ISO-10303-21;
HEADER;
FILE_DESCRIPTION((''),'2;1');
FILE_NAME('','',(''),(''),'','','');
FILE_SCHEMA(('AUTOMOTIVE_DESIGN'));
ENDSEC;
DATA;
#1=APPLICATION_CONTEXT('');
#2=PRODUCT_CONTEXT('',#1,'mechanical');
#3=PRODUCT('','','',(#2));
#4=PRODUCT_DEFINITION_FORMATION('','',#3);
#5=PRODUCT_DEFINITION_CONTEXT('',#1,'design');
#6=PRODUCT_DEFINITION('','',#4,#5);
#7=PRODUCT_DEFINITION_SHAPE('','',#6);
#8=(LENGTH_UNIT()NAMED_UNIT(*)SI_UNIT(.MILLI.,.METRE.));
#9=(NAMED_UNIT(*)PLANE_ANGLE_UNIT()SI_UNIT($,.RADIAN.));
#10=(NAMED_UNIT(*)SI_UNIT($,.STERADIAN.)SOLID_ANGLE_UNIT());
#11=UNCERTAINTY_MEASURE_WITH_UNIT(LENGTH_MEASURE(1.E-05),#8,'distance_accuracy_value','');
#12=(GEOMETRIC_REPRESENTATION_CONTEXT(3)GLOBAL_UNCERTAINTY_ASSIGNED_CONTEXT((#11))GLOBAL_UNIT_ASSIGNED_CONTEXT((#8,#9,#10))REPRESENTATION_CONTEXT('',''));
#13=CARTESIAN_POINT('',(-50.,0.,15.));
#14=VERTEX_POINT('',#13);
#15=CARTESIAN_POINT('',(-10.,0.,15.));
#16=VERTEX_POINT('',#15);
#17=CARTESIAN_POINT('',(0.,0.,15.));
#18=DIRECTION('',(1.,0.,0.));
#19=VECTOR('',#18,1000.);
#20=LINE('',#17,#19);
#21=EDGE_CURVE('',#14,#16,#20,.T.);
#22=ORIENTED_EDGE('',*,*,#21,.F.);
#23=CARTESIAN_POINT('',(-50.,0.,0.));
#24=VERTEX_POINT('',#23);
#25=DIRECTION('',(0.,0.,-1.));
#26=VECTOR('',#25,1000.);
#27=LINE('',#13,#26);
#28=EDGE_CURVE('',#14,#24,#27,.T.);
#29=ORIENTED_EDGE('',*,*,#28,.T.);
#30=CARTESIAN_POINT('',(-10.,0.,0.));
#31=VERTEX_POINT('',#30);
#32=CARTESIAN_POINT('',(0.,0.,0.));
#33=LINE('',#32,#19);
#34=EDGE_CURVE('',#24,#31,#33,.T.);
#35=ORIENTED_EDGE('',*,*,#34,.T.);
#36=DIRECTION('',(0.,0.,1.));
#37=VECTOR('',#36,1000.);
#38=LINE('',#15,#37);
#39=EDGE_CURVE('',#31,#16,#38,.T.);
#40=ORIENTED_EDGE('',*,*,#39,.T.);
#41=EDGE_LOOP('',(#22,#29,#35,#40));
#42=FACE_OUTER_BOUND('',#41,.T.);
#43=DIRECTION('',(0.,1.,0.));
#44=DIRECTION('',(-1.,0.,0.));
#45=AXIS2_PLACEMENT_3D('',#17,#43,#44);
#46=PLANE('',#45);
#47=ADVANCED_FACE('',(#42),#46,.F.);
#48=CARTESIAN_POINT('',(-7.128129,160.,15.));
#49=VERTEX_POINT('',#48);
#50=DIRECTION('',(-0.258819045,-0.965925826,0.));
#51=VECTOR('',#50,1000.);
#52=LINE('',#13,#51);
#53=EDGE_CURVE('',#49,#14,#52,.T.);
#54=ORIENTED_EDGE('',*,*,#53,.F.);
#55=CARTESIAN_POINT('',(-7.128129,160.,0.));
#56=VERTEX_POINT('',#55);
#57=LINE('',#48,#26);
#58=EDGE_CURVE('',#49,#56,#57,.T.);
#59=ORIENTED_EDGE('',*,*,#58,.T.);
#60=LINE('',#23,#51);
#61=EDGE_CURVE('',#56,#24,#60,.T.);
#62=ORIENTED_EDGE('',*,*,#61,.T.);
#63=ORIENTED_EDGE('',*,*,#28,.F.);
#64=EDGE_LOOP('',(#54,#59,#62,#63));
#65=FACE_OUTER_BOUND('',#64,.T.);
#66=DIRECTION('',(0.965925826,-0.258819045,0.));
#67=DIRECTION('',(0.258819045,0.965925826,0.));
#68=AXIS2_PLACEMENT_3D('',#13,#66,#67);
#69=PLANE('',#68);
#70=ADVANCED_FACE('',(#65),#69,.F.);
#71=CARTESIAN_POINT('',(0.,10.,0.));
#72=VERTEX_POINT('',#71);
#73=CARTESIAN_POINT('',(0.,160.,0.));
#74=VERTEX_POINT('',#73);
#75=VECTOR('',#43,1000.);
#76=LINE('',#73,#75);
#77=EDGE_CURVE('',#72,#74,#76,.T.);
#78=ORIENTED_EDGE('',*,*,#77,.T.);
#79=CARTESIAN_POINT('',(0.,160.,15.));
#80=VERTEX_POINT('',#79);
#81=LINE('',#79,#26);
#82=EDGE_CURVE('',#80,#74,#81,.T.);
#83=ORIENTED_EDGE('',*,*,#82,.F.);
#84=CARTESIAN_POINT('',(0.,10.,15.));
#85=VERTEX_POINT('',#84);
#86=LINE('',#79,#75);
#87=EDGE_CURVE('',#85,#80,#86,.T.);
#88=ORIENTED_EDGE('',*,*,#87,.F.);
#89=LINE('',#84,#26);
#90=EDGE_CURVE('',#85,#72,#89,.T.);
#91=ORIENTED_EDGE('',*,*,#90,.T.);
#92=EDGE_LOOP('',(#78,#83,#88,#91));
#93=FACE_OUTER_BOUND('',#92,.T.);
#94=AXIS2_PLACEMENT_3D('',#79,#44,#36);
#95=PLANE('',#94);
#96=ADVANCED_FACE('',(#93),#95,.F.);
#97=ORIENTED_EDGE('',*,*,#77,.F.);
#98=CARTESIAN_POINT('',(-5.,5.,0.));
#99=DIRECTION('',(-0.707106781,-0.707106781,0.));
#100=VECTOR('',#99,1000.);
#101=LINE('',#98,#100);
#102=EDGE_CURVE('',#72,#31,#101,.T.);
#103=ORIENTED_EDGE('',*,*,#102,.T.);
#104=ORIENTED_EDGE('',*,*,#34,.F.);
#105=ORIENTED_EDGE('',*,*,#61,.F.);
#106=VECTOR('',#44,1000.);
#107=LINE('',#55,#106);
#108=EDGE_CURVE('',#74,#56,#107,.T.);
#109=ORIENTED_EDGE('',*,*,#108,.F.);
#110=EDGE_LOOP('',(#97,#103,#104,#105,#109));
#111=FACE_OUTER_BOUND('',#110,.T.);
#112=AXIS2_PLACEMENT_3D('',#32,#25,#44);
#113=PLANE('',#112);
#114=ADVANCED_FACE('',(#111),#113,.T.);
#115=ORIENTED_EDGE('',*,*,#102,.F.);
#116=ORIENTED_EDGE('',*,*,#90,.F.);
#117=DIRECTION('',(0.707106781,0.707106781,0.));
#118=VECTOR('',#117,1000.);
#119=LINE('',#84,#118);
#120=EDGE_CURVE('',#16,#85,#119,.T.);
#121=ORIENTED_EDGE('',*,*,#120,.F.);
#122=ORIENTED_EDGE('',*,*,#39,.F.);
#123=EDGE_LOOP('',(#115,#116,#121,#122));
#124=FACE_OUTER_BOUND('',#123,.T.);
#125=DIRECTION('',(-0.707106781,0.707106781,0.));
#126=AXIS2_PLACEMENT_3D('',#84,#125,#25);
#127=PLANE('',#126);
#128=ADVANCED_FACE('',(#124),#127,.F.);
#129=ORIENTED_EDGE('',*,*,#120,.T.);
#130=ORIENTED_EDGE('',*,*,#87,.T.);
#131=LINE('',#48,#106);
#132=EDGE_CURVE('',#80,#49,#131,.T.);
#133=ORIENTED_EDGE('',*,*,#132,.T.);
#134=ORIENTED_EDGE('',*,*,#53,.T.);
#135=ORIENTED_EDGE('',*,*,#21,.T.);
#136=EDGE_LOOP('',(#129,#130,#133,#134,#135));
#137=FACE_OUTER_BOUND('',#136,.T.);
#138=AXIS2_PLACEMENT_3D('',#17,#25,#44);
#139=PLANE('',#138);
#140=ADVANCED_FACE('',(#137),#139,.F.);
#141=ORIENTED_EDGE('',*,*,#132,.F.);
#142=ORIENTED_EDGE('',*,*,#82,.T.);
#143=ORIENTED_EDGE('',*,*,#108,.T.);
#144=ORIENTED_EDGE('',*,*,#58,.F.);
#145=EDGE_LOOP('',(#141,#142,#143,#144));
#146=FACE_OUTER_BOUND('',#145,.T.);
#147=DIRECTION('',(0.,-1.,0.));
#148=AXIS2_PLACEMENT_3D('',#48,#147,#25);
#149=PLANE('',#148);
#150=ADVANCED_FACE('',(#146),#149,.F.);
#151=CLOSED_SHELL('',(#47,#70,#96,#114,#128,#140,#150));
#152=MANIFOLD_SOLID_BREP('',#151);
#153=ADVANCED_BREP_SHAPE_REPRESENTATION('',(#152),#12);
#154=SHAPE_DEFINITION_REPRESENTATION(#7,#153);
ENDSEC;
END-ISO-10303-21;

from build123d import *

# Parameters (mm, degrees)
GUSSET_PLATE_15MM_DEPTH = 15
EDGE_CHAMFER_10X45_SIZE = 10


with BuildPart() as part:
    # Gusset Profile Sketch → Gusset Plate 15mm (new body)
    with BuildSketch(Plane.XY):
        Polygon((0, 0), (-50, 0), (-7.128129211, 160), (0, 160), align=None)
    extrude(amount=GUSSET_PLATE_15MM_DEPTH)

    # Edge Chamfer 10x45
    edge_chamfer_10x45_edges = [part.edges().sort_by_distance(p)[0] for p in [
        (0, 0, 7.5),
    ]]
    chamfer(edge_chamfer_10x45_edges, length=EDGE_CHAMFER_10X45_SIZE)


solid = part.part
